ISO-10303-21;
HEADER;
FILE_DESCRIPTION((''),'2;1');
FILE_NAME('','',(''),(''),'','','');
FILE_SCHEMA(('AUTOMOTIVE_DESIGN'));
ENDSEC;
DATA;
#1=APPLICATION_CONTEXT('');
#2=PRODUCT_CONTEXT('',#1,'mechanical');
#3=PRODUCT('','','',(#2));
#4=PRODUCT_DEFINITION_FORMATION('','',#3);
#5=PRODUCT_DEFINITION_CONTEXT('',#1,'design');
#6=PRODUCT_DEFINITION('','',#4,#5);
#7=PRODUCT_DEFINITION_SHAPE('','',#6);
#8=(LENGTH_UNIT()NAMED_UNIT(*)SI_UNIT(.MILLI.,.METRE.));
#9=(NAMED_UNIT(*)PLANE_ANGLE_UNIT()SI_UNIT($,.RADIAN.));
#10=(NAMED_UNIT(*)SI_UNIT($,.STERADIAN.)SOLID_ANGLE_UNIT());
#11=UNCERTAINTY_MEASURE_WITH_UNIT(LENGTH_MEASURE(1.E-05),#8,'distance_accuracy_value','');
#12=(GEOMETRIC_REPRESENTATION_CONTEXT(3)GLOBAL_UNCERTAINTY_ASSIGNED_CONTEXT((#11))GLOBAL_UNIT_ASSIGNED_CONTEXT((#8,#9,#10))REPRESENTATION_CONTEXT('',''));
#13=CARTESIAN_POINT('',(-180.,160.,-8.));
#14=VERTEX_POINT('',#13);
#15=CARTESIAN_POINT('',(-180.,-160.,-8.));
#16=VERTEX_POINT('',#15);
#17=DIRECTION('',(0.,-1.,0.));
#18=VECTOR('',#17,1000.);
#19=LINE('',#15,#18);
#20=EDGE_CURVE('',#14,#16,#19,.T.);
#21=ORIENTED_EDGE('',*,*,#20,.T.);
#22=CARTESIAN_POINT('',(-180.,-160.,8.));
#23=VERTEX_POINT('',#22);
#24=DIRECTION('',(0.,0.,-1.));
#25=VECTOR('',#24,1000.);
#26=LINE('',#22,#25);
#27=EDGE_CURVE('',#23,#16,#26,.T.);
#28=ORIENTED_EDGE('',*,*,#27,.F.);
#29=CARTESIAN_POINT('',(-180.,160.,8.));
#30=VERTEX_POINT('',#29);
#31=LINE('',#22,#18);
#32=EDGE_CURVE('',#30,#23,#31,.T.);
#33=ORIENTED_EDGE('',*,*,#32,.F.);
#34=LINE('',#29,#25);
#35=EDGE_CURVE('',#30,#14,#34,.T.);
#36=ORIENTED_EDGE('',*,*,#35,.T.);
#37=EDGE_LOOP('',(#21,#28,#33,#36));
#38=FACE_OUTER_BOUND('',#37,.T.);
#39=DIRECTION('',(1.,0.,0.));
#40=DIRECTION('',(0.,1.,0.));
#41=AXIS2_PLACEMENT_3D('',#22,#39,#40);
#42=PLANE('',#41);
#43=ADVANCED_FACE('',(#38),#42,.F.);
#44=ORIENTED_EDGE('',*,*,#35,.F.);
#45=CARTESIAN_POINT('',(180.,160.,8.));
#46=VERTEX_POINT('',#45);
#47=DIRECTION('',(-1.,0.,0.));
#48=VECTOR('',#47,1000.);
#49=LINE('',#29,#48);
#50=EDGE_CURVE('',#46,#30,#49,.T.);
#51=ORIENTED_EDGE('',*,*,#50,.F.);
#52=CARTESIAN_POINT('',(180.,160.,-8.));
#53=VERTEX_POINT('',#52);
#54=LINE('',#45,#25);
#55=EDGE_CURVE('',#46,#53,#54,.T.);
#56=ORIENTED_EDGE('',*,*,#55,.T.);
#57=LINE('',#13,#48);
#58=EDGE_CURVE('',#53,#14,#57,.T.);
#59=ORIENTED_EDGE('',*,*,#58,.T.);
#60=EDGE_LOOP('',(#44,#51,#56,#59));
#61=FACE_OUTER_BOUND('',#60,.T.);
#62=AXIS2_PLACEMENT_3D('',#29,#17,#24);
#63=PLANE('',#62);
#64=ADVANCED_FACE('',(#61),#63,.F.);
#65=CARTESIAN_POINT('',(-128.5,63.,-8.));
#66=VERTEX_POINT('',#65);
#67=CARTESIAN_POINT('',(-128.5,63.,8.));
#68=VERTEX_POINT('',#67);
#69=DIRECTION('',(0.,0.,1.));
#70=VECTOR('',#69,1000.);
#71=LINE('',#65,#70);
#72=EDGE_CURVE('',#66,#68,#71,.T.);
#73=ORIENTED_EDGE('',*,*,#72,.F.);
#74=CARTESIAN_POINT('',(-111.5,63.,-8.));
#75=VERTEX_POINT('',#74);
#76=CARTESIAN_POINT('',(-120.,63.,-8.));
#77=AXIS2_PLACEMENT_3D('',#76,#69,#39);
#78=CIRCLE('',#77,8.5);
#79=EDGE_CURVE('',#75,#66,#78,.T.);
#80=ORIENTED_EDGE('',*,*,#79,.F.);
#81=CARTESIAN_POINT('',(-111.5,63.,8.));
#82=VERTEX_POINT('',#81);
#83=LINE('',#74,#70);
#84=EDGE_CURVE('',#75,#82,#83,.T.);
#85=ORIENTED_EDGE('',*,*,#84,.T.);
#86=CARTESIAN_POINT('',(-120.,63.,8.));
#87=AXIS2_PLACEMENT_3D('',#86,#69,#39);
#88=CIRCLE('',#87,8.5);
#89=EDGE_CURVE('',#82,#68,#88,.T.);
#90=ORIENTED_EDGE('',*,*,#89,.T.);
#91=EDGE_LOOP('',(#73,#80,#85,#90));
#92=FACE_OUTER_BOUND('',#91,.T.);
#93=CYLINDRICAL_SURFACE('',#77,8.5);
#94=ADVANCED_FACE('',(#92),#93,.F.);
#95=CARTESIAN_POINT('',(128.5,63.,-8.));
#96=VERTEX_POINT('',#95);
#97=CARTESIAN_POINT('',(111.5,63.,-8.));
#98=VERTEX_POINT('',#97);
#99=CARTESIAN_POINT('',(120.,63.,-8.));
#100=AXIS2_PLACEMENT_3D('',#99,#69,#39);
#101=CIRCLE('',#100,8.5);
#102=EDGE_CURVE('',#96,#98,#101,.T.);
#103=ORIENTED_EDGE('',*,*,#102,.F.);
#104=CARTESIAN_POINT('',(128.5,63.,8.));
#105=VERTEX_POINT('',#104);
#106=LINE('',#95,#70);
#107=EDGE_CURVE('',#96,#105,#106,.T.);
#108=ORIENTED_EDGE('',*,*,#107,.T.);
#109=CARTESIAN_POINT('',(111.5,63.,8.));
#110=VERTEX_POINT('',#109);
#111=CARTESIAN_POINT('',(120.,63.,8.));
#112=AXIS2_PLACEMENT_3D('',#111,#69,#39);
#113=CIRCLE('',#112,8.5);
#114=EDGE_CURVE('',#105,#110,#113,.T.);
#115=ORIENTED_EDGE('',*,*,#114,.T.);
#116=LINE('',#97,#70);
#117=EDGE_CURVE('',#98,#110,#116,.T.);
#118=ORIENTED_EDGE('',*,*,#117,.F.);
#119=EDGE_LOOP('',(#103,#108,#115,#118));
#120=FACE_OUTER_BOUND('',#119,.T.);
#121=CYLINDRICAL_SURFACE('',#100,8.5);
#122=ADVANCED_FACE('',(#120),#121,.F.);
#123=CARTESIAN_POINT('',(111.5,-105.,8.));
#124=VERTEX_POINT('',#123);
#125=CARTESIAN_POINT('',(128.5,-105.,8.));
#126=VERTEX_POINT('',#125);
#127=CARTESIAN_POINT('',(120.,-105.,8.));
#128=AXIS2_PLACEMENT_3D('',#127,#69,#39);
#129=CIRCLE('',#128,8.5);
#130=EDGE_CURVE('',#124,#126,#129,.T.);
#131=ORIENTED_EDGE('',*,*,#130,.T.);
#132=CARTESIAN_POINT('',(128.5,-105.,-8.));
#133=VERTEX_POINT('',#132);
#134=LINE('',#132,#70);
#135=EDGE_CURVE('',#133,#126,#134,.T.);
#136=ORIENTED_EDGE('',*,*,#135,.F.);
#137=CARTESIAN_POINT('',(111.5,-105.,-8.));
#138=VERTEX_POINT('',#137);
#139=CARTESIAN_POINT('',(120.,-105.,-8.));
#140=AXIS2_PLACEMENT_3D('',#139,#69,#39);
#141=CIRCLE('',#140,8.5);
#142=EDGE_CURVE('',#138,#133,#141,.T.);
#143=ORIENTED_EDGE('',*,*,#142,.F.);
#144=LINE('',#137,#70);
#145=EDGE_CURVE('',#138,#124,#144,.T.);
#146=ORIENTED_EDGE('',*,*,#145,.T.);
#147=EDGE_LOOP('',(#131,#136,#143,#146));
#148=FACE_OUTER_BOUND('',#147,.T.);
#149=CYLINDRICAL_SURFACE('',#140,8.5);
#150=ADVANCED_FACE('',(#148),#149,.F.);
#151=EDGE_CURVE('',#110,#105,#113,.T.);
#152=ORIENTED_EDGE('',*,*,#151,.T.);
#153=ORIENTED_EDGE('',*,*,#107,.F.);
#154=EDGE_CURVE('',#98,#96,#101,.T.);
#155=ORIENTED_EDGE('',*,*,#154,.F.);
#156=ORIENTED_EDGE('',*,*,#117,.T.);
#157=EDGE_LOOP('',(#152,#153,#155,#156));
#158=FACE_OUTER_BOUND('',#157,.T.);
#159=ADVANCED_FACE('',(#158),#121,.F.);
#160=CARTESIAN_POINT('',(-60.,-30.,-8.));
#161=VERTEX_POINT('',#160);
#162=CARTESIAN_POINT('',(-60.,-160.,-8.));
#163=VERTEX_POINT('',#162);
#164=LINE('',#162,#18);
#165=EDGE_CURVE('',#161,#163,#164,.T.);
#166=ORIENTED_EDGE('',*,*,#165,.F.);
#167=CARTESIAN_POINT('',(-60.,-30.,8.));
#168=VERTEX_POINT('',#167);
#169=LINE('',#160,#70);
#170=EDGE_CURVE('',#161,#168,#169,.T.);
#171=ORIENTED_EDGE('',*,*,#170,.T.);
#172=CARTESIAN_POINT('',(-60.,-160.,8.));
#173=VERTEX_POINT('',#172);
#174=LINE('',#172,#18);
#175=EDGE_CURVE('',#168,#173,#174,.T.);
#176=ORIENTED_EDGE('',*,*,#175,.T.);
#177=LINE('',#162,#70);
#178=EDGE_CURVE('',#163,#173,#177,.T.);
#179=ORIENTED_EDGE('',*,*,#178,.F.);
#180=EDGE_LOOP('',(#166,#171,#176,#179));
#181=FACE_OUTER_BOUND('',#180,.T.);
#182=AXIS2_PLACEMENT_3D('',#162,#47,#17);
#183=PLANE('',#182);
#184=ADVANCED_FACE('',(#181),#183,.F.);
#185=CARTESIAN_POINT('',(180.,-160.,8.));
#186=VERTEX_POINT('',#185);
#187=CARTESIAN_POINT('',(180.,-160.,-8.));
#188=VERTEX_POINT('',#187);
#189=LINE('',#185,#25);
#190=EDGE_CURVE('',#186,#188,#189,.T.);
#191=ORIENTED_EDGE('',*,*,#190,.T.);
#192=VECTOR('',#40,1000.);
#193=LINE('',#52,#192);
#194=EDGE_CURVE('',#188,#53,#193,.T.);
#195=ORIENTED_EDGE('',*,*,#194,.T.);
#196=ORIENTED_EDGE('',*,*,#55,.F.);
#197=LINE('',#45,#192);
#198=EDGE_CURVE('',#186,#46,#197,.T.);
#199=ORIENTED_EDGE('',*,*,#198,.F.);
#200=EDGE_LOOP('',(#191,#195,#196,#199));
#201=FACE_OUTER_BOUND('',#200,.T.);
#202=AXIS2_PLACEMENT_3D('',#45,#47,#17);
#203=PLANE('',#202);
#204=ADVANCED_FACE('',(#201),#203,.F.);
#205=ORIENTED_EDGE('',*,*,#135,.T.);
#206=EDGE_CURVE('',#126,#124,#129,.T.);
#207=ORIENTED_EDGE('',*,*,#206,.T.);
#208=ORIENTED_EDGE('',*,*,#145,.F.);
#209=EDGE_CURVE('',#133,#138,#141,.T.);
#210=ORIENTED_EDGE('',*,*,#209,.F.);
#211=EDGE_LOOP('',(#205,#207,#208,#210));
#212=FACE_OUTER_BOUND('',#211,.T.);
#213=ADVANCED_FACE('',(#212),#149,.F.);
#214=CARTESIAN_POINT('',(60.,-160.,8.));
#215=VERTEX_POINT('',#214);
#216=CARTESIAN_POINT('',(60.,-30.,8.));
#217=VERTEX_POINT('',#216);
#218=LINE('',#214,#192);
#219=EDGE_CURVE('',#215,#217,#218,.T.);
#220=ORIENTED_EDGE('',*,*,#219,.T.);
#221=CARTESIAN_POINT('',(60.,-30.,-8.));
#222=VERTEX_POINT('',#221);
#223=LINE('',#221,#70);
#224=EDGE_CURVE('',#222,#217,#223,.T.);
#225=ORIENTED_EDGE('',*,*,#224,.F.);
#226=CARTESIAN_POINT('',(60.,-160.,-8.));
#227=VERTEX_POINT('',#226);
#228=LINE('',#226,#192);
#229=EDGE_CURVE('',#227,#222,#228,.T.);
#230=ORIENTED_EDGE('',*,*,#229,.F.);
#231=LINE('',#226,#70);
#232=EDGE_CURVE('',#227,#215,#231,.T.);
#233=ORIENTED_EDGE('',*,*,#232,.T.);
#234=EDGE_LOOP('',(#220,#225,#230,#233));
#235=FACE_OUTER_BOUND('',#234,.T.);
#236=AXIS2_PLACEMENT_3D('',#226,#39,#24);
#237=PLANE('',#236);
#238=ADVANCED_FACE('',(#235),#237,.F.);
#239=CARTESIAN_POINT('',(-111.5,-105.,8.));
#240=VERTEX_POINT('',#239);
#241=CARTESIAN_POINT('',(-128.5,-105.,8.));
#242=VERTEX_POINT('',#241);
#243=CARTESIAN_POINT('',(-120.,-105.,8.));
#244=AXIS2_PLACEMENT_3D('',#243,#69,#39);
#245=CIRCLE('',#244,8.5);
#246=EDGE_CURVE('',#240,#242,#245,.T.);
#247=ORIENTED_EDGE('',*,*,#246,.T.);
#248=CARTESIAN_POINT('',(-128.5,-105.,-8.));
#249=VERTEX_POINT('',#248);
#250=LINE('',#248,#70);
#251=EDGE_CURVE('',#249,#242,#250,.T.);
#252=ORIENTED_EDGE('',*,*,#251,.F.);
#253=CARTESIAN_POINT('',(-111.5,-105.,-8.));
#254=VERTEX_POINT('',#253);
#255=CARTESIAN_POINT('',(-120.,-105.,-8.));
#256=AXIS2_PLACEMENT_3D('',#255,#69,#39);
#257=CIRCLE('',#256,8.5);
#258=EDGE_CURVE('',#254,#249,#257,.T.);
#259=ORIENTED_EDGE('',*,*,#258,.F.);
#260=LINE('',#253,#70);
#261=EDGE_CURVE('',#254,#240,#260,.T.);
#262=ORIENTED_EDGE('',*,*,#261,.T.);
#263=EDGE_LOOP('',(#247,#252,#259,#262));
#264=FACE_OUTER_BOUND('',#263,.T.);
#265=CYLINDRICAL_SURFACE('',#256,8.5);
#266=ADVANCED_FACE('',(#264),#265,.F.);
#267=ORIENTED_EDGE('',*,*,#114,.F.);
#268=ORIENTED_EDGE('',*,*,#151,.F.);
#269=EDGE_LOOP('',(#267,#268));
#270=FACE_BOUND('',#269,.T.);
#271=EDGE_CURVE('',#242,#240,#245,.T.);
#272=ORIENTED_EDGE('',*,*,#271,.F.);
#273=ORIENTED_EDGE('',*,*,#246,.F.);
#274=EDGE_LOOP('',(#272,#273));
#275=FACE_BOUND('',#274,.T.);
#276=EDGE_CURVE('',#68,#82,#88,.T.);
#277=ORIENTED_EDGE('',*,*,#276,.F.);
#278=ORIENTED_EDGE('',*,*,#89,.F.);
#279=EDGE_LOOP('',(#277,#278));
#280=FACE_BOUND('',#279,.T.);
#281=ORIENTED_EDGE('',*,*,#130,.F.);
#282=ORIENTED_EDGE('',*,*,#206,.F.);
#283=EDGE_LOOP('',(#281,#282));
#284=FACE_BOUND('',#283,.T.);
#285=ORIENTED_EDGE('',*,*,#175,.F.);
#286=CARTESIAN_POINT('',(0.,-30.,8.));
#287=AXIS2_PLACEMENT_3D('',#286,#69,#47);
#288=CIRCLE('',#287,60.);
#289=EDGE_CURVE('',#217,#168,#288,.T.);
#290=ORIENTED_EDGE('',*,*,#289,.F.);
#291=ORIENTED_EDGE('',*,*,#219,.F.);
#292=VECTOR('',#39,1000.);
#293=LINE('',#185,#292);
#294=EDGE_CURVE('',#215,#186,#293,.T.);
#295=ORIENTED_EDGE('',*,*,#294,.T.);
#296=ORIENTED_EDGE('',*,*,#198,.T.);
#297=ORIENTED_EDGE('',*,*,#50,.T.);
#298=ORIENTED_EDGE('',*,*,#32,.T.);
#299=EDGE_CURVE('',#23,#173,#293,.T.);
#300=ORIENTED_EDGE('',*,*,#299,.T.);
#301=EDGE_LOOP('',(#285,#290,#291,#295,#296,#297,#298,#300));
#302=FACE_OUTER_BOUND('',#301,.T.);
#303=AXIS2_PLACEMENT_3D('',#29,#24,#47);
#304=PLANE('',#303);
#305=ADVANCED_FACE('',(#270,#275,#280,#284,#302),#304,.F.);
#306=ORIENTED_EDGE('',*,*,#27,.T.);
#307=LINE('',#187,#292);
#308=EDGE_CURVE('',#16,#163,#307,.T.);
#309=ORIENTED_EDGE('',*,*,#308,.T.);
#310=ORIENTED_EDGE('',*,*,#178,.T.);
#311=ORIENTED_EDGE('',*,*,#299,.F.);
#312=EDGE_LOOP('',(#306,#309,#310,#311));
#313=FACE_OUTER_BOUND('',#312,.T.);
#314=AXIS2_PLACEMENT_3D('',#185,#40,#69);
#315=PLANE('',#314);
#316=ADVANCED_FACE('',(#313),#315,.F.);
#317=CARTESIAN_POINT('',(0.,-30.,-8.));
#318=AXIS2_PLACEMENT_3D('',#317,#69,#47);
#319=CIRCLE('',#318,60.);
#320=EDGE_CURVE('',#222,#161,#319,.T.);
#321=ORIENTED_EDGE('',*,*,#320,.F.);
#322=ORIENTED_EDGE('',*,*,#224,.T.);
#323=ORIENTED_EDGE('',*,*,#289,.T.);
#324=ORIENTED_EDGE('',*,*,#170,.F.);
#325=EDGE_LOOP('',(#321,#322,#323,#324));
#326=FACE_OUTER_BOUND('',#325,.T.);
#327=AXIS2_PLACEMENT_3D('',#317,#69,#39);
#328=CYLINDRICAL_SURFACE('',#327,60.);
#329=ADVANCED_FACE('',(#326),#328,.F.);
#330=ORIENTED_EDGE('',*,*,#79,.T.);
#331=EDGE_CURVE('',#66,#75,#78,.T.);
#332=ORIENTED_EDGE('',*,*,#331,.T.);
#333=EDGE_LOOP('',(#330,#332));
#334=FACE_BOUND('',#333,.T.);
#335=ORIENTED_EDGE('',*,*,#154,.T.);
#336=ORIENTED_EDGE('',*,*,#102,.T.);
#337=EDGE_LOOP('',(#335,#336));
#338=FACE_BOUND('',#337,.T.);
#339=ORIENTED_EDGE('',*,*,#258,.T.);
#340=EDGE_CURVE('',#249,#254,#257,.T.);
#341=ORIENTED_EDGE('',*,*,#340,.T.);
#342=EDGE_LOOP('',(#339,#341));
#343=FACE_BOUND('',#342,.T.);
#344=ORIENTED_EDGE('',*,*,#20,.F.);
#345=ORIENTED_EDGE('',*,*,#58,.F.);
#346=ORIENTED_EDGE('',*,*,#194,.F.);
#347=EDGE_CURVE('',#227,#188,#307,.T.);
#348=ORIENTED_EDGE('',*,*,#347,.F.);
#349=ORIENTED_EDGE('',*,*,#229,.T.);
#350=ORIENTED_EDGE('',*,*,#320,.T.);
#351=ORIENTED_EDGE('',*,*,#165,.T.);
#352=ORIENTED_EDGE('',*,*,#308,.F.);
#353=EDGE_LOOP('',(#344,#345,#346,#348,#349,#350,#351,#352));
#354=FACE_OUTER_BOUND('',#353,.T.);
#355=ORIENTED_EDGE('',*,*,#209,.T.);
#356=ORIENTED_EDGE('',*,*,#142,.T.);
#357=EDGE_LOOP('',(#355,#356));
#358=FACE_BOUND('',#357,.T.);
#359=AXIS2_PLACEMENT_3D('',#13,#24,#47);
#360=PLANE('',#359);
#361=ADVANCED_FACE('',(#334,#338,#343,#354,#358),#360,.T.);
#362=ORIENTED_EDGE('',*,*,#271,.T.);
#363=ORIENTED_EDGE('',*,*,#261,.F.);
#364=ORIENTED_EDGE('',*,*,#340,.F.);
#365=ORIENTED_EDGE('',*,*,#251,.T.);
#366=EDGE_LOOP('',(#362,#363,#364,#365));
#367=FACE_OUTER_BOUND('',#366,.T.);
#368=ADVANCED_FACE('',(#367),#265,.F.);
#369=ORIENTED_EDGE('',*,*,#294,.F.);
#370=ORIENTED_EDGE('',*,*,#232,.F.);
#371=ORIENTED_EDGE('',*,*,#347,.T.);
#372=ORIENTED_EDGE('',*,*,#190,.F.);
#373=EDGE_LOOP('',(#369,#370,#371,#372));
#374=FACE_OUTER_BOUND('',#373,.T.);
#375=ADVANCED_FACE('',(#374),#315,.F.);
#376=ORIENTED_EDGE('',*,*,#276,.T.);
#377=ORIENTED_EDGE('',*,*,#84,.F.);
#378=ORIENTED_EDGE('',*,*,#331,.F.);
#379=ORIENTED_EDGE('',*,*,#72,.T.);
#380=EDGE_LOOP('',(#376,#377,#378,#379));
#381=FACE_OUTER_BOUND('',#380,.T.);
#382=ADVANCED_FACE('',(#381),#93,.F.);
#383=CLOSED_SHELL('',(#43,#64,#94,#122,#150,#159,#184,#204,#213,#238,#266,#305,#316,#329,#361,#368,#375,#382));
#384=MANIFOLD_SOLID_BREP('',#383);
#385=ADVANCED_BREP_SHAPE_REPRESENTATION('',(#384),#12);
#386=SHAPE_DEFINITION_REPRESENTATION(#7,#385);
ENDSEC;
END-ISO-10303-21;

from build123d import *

# Parameters (mm, degrees)
SKETCH1_W            = 360
SKETCH1_H            = 320
EXTRUDE1_DEPTH       = 8
EXTRUDE2_DEPTH       = 16
SKETCH3_R            = 8.5
EXTRUDE3_DEPTH       = 16
LPATTERN1_COUNT      = 2
LPATTERN1_PITCH      = 240
LPATTERN1_COUNT_DIR2 = 2
LPATTERN1_PITCH_DIR2 = 168


with BuildPart() as part:
    # Sketch1 → Extrude1 (new, symmetric)
    with BuildSketch(Plane.XY):
        Rectangle(SKETCH1_W, SKETCH1_H)
    extrude(amount=EXTRUDE1_DEPTH, both=True)

    # Sketch2 → Extrude2 (cut)
    with BuildSketch(Plane.XY.offset(8)):
        with BuildLine():
            Line((-60, -160), (-60, -30))
            ThreePointArc((-60, -30), (0, 30), (60, -30))
            Line((60, -30), (60, -160))
            Line((60, -160), (-60, -160))
        make_face()
    extrude(amount=-EXTRUDE2_DEPTH, mode=Mode.SUBTRACT)

    # Sketch3 → Extrude3 (cut)
    with BuildSketch(Plane.XY.offset(8)):
        with Locations((-120, 63)):
            Circle(SKETCH3_R)
    extrude3 = extrude(amount=-EXTRUDE3_DEPTH, mode=Mode.SUBTRACT)

    # LPattern1: Extrude3 2 × 2
    with Locations(*[(i * LPATTERN1_PITCH, -j * LPATTERN1_PITCH_DIR2, 0) for i in range(LPATTERN1_COUNT) for j in range(LPATTERN1_COUNT_DIR2) if (i, j) != (0, 0)]):
        add(extrude3, mode=Mode.SUBTRACT)


solid = part.part
